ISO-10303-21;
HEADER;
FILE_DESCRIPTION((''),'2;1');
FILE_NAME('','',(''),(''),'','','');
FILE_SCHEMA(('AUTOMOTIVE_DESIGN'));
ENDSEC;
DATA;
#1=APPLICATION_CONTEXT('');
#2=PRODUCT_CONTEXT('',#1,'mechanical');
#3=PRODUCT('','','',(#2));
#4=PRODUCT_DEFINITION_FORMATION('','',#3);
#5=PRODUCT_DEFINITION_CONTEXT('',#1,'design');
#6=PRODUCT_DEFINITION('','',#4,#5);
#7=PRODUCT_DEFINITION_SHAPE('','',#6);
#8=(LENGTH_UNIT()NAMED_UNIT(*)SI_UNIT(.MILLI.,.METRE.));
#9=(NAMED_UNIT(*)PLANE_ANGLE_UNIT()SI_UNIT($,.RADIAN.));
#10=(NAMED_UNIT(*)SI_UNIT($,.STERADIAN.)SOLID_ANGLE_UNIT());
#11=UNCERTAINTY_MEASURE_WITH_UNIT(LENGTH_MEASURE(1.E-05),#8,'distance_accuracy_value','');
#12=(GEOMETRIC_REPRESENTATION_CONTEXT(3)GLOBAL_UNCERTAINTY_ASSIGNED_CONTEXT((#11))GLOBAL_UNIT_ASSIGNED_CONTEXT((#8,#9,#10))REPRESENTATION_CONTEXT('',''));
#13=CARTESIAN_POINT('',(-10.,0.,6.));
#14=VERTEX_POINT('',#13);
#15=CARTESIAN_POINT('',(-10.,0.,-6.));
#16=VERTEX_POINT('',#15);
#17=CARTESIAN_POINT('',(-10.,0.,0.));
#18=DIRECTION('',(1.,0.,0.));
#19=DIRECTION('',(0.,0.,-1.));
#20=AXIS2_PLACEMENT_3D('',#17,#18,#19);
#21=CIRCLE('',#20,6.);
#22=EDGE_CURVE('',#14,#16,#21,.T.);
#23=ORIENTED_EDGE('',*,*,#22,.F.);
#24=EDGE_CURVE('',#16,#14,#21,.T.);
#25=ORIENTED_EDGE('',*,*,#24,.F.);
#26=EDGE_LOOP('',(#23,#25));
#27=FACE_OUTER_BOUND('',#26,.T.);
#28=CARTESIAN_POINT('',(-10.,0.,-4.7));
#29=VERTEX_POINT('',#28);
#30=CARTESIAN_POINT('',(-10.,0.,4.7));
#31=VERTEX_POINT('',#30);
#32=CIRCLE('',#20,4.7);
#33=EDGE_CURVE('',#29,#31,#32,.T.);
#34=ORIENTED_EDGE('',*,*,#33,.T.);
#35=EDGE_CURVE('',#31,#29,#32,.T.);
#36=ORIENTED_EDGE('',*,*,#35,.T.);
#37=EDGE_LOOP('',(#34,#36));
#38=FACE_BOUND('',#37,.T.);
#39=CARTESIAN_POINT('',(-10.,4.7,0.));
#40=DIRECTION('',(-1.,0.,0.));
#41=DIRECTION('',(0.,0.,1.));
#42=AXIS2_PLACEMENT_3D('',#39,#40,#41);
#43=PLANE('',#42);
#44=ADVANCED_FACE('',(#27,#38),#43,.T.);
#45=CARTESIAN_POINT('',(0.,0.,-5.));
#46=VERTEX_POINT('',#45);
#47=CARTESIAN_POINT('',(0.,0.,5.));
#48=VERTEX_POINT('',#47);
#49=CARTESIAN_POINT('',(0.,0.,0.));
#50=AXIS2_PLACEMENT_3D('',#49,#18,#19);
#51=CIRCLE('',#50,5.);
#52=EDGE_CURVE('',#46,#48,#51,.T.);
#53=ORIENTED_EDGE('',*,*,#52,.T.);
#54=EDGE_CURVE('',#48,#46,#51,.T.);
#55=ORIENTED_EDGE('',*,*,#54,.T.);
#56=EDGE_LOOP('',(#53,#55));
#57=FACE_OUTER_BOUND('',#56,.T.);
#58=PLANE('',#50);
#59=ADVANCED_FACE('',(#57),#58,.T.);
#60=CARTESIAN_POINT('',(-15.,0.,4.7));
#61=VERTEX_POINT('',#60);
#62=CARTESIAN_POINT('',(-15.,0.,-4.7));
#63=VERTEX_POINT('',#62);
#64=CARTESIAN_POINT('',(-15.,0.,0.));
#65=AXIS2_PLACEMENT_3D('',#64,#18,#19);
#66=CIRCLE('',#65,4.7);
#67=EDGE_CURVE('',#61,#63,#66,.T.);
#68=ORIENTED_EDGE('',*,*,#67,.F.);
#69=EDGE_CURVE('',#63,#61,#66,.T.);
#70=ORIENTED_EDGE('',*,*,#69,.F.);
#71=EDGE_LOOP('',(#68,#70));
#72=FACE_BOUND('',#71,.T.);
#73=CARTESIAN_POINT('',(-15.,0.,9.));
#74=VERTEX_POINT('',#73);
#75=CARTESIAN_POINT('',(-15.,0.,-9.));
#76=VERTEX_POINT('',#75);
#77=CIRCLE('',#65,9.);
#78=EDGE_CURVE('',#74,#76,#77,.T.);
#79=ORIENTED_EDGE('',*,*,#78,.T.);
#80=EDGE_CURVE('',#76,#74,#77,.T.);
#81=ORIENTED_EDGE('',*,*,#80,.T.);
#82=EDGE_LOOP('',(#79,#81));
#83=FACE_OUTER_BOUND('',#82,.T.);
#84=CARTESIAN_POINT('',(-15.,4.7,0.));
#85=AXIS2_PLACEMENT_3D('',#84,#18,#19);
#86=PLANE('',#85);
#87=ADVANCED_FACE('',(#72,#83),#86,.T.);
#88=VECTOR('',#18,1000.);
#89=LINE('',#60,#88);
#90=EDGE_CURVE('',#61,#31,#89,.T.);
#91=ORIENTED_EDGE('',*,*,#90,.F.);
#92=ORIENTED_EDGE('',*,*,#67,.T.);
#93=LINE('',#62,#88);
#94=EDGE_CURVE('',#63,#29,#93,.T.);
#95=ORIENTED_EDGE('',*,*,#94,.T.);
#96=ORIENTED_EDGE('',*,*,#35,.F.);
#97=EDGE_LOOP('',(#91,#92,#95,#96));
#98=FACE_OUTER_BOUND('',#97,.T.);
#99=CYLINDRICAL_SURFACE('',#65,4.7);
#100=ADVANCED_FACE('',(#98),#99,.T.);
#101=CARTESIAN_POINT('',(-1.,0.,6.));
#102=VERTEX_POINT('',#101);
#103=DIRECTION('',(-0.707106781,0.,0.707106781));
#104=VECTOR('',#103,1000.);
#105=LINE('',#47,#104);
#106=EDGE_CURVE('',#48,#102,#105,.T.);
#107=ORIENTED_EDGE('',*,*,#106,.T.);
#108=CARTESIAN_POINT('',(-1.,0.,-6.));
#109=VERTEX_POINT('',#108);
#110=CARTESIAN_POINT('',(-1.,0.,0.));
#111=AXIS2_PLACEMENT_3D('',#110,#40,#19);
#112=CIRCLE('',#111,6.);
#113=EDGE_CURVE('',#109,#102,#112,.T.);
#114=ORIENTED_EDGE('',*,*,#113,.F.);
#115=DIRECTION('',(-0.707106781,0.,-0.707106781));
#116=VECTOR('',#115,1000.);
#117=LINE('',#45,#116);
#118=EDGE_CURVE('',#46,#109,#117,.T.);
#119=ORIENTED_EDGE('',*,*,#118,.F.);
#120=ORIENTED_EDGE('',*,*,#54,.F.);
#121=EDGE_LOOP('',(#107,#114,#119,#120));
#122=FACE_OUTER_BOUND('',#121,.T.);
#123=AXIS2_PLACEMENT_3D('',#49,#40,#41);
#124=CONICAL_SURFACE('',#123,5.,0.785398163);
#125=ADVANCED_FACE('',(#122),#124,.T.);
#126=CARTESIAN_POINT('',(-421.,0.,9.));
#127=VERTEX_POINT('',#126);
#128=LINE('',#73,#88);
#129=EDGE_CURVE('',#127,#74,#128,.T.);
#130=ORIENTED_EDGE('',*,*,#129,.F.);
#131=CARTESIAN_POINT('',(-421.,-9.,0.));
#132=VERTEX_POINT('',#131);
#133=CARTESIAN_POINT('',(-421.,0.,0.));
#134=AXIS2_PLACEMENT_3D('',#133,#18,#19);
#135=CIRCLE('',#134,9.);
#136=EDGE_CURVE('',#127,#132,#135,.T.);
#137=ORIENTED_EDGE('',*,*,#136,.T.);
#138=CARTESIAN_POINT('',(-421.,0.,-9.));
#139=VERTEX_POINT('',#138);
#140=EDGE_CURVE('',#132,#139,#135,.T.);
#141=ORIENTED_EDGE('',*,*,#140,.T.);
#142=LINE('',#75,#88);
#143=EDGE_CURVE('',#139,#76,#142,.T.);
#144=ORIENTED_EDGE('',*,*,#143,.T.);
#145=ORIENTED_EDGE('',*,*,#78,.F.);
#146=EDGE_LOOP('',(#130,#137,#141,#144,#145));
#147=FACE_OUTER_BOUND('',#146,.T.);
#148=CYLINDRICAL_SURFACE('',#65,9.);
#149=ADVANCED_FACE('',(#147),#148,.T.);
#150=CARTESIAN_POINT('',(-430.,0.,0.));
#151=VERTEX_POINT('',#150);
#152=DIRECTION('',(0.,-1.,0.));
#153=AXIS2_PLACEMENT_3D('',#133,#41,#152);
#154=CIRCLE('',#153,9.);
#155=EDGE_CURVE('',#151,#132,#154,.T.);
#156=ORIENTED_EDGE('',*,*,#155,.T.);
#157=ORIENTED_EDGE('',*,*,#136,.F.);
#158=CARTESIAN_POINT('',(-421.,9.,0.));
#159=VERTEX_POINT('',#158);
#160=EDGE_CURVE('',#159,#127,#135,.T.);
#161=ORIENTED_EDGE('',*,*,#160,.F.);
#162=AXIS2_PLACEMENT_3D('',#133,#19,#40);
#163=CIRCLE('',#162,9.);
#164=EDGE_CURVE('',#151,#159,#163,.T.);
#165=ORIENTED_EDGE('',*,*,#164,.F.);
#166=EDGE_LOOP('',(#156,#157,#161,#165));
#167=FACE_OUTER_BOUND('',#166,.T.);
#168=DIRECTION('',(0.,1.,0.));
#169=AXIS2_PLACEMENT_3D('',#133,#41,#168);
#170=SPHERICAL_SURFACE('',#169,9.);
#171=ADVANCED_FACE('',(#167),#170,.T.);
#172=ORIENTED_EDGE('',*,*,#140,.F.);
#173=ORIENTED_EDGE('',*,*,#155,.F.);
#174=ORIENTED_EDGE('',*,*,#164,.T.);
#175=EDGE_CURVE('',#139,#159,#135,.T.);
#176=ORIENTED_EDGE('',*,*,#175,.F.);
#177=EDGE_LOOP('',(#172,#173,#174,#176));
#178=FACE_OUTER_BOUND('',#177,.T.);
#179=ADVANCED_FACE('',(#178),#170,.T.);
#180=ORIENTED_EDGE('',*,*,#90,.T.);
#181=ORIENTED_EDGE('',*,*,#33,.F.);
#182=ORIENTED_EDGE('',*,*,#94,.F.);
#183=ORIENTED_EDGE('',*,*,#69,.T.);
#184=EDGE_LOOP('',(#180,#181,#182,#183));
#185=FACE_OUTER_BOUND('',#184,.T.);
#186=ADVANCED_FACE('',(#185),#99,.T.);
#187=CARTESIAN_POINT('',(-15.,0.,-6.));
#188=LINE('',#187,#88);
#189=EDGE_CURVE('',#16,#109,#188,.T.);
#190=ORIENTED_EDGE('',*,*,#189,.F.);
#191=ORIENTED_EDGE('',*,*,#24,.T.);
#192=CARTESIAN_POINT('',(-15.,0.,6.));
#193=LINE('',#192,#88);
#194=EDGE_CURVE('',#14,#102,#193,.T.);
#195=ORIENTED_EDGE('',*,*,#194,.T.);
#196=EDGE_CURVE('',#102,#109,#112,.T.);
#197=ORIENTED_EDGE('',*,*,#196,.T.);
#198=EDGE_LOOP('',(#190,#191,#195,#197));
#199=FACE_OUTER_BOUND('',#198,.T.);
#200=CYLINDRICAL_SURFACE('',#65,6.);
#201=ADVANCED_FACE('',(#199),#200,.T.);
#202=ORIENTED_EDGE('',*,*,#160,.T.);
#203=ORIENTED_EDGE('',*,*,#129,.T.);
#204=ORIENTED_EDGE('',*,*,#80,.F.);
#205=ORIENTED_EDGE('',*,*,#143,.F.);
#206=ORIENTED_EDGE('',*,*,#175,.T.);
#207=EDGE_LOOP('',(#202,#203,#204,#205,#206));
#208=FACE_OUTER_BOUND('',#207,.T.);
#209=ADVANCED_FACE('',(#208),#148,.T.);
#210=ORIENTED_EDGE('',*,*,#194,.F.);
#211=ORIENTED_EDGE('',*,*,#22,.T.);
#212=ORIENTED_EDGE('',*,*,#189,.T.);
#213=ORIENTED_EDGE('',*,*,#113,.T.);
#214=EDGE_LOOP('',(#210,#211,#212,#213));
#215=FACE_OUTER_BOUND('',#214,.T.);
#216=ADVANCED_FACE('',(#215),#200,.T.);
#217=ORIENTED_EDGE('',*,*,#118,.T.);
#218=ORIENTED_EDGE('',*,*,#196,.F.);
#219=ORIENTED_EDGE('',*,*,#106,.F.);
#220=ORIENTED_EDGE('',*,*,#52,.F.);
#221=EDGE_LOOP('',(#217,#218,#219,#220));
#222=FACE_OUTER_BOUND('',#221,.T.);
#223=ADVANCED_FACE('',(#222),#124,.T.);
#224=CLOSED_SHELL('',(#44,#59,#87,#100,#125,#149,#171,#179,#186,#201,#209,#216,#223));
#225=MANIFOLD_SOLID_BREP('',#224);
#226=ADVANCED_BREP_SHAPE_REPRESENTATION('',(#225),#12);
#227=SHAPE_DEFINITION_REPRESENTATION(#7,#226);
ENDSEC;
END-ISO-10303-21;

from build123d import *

# Parameters (mm, degrees)
CHAMFER1_SIZE = 1


with BuildPart() as part:
    # Sketch1 → Revolve2 (revolve)
    with BuildSketch(Plane.XY, mode=Mode.PRIVATE) as revolve2_sk:
        with BuildLine():
            Line((0, 0), (-10, 0))
            Line((-10, 0), (-15, 0))
            Line((-15, 0), (-430, 0))
            ThreePointArc((-430, 0), (-427.363961031, 6.363961031), (-421, 9))
            Line((-421, 9), (-15, 9))
            Line((-15, 9), (-15, 4.7))
            Line((-15, 4.7), (-10, 4.7))
            Line((-10, 4.7), (-10, 6))
            Line((-10, 6), (0, 6))
            Line((0, 6), (0, 0))
        make_face()
    revolve(revolve2_sk.sketch.rotate(Axis((-15, 0, 0), (-1, 0, 0)), 90), axis=Axis((-15, 0, 0), (-1, 0, 0)))

    # Chamfer1
    chamfer1_edges = [part.edges().sort_by_distance(p)[0] for p in [
        (0, 0, 6),
    ]]
    chamfer(chamfer1_edges, length=CHAMFER1_SIZE)


solid = part.part
